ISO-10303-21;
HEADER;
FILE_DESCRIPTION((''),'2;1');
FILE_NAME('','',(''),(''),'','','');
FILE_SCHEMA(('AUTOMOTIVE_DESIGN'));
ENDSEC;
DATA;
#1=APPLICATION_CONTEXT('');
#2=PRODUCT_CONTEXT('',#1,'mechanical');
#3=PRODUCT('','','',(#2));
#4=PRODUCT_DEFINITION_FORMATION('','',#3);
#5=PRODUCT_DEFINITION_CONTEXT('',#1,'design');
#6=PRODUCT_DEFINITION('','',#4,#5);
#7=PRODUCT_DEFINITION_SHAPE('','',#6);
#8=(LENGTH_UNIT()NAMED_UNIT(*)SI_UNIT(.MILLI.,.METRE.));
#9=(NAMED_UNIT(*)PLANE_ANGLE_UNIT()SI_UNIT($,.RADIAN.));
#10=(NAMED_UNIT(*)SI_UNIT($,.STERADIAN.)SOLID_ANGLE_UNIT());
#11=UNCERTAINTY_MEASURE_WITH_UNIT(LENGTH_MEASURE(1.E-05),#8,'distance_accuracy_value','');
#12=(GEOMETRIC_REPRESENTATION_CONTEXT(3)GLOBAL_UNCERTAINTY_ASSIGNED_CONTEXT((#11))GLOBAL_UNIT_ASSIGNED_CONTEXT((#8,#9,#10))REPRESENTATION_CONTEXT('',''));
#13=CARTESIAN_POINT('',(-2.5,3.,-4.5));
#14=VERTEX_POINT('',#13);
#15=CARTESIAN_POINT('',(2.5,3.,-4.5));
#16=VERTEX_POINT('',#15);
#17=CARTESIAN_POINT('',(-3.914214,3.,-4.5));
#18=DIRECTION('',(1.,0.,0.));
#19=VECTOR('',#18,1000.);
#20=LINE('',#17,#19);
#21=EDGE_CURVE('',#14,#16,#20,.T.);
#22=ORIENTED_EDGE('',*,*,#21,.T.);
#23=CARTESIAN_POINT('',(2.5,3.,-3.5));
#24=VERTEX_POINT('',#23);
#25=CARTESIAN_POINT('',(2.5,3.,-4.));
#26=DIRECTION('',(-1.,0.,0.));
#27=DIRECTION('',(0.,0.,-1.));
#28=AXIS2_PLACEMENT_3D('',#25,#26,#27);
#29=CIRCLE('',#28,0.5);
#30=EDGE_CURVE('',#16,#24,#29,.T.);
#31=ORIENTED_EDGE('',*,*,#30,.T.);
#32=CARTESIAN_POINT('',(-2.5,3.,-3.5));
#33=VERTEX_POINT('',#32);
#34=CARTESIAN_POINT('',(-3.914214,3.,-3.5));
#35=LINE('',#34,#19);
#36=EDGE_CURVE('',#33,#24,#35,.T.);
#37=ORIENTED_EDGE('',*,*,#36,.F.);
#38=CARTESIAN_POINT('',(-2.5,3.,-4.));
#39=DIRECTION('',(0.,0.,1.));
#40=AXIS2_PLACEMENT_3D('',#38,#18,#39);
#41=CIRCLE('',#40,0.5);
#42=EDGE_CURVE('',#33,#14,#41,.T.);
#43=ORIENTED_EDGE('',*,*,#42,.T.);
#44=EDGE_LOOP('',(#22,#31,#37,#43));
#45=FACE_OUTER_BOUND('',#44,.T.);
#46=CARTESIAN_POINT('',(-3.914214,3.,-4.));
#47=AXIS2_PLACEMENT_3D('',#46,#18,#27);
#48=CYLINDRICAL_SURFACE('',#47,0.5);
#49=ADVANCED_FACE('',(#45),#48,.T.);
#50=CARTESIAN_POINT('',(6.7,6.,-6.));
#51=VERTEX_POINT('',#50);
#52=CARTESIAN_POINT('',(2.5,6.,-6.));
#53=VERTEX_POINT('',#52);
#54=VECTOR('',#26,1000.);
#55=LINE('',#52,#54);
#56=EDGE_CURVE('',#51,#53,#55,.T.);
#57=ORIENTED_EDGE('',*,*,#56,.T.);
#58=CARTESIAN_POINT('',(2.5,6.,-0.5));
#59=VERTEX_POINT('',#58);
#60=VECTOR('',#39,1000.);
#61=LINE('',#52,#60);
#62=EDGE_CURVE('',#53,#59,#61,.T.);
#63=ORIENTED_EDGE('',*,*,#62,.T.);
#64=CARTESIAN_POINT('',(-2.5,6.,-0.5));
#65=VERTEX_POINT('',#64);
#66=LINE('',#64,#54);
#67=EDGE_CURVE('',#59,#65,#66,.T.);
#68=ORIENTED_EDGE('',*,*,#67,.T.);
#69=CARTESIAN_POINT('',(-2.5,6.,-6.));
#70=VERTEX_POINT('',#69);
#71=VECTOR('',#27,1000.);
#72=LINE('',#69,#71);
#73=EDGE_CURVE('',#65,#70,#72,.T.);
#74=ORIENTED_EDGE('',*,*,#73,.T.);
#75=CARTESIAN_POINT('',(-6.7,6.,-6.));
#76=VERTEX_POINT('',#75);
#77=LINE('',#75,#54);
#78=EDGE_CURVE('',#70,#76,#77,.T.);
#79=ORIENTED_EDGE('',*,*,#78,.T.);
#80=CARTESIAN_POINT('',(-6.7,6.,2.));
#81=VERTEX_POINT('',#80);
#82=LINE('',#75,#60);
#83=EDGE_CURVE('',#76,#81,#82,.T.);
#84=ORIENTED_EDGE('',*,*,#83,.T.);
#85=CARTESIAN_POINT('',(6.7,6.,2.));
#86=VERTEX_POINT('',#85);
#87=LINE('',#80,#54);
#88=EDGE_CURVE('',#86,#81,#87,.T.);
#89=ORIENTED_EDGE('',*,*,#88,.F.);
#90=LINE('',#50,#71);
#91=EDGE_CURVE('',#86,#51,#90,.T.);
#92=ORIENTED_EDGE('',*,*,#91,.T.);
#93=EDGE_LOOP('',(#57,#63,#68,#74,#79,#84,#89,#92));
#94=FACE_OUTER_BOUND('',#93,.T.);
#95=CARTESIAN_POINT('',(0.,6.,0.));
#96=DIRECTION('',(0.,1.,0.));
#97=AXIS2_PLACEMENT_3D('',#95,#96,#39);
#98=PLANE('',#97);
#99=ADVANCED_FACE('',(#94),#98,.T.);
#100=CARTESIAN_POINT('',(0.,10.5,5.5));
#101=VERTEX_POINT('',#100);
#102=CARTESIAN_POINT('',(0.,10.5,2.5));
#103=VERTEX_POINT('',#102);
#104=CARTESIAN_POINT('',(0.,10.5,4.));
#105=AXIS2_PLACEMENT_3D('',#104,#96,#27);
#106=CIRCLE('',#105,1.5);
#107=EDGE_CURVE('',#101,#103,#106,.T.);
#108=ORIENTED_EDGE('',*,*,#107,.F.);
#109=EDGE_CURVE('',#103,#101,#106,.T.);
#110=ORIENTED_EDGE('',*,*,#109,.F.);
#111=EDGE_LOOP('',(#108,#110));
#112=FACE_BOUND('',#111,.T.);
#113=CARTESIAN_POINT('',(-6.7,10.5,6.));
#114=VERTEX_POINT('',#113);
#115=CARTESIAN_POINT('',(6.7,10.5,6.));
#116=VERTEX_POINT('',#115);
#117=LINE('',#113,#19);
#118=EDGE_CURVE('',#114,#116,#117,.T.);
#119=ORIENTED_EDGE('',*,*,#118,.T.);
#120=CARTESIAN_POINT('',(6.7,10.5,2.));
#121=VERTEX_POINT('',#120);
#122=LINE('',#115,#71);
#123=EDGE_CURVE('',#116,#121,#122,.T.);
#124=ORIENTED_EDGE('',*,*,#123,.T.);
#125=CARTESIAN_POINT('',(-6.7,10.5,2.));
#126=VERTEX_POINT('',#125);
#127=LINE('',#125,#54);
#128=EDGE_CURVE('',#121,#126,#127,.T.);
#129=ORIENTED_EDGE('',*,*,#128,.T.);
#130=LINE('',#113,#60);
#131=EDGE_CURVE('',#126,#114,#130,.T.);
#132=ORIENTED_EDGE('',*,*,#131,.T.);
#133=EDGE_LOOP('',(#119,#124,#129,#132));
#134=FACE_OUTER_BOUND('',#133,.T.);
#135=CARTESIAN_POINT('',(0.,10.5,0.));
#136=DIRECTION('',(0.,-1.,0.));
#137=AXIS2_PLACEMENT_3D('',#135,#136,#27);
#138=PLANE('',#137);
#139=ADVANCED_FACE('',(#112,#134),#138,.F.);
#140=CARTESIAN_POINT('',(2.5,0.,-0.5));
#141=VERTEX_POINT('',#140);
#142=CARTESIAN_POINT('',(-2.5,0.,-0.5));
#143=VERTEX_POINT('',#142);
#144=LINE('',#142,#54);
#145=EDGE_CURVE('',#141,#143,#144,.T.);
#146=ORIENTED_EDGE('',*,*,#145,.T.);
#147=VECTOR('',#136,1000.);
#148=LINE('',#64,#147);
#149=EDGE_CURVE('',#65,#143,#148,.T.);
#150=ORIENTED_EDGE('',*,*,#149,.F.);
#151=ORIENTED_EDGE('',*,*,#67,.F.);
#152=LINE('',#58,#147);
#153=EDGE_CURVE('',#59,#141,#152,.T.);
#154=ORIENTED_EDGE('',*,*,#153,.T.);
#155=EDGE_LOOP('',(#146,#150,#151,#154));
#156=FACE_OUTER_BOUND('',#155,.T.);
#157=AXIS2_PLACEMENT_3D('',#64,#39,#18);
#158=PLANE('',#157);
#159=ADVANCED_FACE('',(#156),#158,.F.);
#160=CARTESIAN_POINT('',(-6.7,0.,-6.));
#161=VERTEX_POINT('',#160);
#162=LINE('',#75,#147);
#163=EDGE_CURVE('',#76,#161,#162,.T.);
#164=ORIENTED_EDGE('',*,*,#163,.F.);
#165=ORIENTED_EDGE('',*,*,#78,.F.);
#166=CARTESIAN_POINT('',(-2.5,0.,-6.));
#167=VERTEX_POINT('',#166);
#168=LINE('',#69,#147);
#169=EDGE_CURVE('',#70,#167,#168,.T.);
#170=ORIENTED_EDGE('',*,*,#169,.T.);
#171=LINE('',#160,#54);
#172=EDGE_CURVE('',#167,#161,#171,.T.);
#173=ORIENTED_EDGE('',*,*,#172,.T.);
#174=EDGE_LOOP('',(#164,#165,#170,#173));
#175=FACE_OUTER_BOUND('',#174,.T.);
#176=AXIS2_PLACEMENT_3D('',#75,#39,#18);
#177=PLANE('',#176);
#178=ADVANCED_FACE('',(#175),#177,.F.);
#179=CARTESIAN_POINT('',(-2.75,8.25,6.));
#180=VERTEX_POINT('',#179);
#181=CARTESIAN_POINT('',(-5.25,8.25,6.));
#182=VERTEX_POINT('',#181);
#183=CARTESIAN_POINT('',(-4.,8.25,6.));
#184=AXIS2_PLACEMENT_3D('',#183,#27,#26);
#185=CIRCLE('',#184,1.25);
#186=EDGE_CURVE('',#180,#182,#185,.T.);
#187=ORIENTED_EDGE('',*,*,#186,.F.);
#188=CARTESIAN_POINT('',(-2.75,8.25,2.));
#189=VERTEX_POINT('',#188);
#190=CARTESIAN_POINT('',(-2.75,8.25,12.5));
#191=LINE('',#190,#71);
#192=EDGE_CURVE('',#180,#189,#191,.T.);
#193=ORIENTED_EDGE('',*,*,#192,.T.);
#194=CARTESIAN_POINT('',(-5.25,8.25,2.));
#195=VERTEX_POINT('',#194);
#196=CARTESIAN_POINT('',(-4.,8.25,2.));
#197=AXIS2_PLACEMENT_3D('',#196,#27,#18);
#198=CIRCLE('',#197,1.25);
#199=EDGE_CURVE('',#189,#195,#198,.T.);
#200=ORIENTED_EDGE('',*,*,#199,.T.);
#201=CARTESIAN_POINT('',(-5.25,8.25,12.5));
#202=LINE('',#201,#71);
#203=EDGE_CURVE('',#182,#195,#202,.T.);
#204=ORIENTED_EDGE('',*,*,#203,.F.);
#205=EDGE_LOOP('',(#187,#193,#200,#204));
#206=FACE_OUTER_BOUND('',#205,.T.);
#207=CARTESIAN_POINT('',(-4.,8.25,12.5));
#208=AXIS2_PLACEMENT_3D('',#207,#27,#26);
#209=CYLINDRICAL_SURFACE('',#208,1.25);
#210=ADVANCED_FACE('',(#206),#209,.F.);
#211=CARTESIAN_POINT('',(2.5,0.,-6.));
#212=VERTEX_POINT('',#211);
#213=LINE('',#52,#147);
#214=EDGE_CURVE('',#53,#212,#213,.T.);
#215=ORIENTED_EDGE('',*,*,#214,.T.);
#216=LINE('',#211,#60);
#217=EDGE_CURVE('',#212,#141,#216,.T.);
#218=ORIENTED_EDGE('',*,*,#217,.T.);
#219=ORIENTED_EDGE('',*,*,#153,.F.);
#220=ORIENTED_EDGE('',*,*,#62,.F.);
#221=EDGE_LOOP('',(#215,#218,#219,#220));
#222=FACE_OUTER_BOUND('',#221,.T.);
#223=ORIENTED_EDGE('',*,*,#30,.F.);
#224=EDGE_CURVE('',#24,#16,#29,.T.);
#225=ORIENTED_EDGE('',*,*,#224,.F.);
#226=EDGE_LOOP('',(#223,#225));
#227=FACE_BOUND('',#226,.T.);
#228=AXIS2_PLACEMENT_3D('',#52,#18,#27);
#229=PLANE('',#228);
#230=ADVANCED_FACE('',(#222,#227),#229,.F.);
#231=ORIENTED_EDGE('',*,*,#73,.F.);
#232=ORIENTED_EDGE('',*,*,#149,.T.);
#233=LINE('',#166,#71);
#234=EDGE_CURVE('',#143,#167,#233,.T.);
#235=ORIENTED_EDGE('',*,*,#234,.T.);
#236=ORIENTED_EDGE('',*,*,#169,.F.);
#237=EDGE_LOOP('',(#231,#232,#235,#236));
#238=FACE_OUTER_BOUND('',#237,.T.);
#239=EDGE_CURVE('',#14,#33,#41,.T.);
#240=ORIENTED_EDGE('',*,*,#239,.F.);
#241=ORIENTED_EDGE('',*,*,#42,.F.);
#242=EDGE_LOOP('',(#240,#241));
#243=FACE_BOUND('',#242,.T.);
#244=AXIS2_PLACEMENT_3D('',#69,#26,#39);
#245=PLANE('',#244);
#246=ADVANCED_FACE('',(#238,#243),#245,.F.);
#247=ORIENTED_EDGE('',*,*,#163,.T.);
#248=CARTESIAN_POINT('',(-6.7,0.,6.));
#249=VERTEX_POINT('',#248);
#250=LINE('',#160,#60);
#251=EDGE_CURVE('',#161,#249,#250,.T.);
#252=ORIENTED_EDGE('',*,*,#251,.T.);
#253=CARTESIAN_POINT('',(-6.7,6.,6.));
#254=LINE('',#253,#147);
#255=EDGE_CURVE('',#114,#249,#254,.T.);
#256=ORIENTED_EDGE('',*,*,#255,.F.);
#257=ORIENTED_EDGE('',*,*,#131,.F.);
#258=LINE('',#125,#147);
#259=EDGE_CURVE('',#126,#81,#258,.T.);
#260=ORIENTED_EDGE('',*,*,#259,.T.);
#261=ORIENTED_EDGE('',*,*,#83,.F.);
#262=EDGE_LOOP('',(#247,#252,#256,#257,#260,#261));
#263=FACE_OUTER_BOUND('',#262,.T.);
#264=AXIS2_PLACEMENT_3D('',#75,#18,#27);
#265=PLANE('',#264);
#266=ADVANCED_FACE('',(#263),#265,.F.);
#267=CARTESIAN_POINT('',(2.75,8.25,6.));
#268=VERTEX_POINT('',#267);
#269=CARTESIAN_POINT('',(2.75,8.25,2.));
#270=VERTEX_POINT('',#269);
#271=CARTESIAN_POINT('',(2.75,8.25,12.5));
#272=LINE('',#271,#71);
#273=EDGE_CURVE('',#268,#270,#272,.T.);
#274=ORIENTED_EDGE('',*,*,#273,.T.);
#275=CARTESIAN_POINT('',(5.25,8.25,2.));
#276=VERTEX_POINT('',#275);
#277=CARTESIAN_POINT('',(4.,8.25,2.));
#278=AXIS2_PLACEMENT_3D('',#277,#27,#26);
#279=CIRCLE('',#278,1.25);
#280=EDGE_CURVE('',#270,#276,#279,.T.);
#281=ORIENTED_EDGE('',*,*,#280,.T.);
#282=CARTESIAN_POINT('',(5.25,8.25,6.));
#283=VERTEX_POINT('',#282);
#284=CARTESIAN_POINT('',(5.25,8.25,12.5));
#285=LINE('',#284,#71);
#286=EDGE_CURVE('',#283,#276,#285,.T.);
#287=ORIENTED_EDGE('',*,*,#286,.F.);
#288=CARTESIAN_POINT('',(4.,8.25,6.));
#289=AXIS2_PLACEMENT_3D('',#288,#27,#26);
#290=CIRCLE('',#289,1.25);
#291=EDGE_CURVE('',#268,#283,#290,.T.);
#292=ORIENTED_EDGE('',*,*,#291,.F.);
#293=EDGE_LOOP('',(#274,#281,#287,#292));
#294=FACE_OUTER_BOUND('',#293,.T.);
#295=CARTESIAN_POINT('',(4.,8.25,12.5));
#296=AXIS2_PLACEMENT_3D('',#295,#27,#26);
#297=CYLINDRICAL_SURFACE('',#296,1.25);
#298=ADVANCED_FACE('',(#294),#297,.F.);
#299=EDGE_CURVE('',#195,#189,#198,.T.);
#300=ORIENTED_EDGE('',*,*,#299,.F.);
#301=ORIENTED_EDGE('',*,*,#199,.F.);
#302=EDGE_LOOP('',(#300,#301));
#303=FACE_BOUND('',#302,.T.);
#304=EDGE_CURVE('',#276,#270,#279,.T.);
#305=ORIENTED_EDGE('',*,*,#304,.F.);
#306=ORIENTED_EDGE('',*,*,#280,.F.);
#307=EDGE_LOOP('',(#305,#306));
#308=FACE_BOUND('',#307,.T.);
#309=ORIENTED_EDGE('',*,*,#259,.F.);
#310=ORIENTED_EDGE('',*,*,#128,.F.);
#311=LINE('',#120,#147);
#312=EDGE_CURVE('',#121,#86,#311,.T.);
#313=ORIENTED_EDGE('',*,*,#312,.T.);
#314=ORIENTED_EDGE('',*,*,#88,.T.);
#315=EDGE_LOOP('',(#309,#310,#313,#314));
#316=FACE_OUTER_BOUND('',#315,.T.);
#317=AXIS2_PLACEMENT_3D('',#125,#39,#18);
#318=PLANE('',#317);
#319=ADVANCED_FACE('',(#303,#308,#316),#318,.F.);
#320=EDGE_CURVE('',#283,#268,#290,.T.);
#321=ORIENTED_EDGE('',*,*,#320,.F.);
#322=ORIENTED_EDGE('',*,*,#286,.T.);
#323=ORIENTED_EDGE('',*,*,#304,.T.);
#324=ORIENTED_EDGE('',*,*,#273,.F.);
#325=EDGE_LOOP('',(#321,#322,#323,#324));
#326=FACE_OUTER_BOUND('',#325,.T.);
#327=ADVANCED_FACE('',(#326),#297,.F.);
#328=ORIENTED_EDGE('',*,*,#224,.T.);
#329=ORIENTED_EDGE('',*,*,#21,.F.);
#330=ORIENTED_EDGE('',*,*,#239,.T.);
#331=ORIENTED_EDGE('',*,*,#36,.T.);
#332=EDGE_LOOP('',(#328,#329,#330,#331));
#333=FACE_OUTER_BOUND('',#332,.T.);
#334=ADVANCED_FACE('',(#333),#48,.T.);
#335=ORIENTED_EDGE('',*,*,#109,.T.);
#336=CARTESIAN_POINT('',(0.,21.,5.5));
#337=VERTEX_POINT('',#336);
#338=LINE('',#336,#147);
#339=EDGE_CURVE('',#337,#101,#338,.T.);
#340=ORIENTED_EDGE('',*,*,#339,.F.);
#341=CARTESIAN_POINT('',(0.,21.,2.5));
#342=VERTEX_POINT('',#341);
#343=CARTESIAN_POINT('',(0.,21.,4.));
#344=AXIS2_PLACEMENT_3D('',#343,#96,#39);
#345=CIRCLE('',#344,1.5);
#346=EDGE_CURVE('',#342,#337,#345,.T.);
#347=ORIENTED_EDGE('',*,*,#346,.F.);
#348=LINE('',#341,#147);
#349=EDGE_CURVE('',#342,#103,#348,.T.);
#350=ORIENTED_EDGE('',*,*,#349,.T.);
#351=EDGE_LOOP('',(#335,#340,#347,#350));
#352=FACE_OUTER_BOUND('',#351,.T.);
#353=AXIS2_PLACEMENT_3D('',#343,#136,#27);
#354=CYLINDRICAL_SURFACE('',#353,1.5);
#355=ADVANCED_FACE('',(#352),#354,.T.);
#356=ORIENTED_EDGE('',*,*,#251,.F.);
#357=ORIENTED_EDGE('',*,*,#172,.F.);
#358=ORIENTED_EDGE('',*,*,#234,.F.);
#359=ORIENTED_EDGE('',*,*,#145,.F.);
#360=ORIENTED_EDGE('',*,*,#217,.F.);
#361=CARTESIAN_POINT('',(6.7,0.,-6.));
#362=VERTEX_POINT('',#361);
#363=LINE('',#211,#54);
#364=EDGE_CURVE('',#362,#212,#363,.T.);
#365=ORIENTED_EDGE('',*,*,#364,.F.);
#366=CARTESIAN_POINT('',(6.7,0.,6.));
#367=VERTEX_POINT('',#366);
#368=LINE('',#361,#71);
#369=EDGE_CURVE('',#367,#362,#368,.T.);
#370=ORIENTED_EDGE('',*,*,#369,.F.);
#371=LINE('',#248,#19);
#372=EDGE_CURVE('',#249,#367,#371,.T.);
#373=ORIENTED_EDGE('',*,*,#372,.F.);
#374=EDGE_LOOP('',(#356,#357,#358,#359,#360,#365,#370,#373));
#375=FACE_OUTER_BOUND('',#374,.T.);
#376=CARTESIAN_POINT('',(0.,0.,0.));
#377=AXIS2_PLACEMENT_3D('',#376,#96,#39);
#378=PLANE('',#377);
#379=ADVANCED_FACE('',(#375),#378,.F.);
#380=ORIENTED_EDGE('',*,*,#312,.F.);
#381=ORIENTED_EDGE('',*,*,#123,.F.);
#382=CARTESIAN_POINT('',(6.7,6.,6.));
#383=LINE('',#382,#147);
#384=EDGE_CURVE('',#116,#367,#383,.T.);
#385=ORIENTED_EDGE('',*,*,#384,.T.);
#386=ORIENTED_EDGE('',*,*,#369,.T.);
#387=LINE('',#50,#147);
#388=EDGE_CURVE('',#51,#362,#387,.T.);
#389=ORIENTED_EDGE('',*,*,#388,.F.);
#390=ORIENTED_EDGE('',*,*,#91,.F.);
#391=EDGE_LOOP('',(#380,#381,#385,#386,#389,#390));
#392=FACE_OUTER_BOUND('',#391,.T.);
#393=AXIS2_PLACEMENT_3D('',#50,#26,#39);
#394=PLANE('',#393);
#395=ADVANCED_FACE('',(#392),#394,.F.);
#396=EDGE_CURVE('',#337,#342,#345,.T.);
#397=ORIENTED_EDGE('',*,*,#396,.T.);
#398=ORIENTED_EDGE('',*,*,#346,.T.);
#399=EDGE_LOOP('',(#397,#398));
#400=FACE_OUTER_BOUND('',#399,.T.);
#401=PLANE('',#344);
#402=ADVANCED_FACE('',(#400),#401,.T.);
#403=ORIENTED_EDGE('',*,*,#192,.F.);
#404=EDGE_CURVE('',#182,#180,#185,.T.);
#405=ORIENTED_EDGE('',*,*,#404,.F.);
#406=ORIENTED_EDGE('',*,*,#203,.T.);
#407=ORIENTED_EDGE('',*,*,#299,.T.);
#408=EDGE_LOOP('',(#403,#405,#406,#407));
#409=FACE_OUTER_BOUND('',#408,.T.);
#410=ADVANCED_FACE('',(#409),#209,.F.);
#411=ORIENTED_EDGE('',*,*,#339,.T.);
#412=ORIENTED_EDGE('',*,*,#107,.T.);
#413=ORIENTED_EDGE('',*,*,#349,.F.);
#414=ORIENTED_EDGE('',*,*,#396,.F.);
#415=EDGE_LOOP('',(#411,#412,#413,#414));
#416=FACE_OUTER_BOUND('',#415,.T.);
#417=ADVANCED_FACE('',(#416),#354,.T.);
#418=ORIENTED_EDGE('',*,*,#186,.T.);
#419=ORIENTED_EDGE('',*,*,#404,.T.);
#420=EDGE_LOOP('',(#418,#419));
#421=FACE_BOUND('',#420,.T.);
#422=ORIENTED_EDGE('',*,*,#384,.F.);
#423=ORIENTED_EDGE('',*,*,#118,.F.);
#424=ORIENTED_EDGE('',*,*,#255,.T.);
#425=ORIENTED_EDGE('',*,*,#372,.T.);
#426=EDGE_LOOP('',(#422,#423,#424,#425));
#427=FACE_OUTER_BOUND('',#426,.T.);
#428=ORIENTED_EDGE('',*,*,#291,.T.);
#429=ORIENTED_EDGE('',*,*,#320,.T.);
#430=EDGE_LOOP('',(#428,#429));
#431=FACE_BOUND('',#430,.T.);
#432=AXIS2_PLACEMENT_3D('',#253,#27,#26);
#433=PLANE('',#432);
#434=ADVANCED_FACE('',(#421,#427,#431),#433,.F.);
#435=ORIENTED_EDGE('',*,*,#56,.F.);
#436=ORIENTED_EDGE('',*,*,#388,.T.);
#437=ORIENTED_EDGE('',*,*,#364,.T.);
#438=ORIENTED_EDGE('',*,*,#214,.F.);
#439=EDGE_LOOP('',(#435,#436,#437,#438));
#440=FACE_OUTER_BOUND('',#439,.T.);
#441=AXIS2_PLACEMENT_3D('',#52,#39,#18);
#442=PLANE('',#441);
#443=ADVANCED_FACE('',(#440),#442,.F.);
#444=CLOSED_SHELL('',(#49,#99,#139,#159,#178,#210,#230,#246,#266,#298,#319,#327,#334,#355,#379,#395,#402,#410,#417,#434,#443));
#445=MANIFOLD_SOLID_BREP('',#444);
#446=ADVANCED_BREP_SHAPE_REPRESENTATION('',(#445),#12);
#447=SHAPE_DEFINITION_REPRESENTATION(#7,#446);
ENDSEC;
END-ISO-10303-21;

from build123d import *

# Parameters (mm, degrees)
BOSS_EXTRUDE1_DEPTH = 6
SKETCH2_W           = 13.4
SKETCH2_H           = 4
BOSS_EXTRUDE2_DEPTH = 4.5
SKETCH3_R           = 1.5
BOSS_EXTRUDE3_DEPTH = 10.5
SKETCH4_R           = 1.25
CUT_EXTRUDE1_DEPTH  = 10.5
SKETCH5_R           = 0.5
BOSS_EXTRUDE4_DEPTH = 5


with BuildPart() as part:
    # Sketch1 → Boss-Extrude1 (new body)
    with BuildSketch(Plane(origin=(0, 0, 0), x_dir=(1, 0, 0), z_dir=(0, 1, 0))):
        Polygon((2.5, 6), (6.7, 6), (6.7, -6), (-6.7, -6), (-6.7, 6), (-2.5, 6), (-2.5, 0.5), (2.5, 0.5), align=None)
    extrude(amount=BOSS_EXTRUDE1_DEPTH)

    # Sketch2 → Boss-Extrude2 (add)
    with BuildSketch(Plane(origin=(0, 6, 0), x_dir=(1, 0, 0), z_dir=(0, 1, 0))):
        with Locations((0, -4)):
            Rectangle(SKETCH2_W, SKETCH2_H)
    extrude(amount=BOSS_EXTRUDE2_DEPTH)

    # Sketch3 → Boss-Extrude3 (add)
    with BuildSketch(Plane(origin=(0, 10.5, 0), x_dir=(1, 0, 0), z_dir=(0, 1, 0))):
        with Locations(Location((0, -4, 0), (0, 0, 90))):
            Circle(SKETCH3_R)
    extrude(amount=BOSS_EXTRUDE3_DEPTH)

    # Sketch4 → Cut-Extrude1 (cut)
    with BuildSketch(Plane(origin=(0, 0, 2), x_dir=(-1, 0, 0), z_dir=(0, 0, -1))):
        with Locations((-4, 8.25)):
            Circle(SKETCH4_R)
        with Locations((4, 8.25)):
            Circle(SKETCH4_R)
    extrude(amount=-CUT_EXTRUDE1_DEPTH, mode=Mode.SUBTRACT)

    # Sketch5 → Boss-Extrude4 (add)
    with BuildSketch(Plane.ZY.offset(-2.5)):
        with Locations(Location((-4, 3, 0), (0, 0, 180))):
            Circle(SKETCH5_R)
    extrude(amount=BOSS_EXTRUDE4_DEPTH)


solid = part.part
